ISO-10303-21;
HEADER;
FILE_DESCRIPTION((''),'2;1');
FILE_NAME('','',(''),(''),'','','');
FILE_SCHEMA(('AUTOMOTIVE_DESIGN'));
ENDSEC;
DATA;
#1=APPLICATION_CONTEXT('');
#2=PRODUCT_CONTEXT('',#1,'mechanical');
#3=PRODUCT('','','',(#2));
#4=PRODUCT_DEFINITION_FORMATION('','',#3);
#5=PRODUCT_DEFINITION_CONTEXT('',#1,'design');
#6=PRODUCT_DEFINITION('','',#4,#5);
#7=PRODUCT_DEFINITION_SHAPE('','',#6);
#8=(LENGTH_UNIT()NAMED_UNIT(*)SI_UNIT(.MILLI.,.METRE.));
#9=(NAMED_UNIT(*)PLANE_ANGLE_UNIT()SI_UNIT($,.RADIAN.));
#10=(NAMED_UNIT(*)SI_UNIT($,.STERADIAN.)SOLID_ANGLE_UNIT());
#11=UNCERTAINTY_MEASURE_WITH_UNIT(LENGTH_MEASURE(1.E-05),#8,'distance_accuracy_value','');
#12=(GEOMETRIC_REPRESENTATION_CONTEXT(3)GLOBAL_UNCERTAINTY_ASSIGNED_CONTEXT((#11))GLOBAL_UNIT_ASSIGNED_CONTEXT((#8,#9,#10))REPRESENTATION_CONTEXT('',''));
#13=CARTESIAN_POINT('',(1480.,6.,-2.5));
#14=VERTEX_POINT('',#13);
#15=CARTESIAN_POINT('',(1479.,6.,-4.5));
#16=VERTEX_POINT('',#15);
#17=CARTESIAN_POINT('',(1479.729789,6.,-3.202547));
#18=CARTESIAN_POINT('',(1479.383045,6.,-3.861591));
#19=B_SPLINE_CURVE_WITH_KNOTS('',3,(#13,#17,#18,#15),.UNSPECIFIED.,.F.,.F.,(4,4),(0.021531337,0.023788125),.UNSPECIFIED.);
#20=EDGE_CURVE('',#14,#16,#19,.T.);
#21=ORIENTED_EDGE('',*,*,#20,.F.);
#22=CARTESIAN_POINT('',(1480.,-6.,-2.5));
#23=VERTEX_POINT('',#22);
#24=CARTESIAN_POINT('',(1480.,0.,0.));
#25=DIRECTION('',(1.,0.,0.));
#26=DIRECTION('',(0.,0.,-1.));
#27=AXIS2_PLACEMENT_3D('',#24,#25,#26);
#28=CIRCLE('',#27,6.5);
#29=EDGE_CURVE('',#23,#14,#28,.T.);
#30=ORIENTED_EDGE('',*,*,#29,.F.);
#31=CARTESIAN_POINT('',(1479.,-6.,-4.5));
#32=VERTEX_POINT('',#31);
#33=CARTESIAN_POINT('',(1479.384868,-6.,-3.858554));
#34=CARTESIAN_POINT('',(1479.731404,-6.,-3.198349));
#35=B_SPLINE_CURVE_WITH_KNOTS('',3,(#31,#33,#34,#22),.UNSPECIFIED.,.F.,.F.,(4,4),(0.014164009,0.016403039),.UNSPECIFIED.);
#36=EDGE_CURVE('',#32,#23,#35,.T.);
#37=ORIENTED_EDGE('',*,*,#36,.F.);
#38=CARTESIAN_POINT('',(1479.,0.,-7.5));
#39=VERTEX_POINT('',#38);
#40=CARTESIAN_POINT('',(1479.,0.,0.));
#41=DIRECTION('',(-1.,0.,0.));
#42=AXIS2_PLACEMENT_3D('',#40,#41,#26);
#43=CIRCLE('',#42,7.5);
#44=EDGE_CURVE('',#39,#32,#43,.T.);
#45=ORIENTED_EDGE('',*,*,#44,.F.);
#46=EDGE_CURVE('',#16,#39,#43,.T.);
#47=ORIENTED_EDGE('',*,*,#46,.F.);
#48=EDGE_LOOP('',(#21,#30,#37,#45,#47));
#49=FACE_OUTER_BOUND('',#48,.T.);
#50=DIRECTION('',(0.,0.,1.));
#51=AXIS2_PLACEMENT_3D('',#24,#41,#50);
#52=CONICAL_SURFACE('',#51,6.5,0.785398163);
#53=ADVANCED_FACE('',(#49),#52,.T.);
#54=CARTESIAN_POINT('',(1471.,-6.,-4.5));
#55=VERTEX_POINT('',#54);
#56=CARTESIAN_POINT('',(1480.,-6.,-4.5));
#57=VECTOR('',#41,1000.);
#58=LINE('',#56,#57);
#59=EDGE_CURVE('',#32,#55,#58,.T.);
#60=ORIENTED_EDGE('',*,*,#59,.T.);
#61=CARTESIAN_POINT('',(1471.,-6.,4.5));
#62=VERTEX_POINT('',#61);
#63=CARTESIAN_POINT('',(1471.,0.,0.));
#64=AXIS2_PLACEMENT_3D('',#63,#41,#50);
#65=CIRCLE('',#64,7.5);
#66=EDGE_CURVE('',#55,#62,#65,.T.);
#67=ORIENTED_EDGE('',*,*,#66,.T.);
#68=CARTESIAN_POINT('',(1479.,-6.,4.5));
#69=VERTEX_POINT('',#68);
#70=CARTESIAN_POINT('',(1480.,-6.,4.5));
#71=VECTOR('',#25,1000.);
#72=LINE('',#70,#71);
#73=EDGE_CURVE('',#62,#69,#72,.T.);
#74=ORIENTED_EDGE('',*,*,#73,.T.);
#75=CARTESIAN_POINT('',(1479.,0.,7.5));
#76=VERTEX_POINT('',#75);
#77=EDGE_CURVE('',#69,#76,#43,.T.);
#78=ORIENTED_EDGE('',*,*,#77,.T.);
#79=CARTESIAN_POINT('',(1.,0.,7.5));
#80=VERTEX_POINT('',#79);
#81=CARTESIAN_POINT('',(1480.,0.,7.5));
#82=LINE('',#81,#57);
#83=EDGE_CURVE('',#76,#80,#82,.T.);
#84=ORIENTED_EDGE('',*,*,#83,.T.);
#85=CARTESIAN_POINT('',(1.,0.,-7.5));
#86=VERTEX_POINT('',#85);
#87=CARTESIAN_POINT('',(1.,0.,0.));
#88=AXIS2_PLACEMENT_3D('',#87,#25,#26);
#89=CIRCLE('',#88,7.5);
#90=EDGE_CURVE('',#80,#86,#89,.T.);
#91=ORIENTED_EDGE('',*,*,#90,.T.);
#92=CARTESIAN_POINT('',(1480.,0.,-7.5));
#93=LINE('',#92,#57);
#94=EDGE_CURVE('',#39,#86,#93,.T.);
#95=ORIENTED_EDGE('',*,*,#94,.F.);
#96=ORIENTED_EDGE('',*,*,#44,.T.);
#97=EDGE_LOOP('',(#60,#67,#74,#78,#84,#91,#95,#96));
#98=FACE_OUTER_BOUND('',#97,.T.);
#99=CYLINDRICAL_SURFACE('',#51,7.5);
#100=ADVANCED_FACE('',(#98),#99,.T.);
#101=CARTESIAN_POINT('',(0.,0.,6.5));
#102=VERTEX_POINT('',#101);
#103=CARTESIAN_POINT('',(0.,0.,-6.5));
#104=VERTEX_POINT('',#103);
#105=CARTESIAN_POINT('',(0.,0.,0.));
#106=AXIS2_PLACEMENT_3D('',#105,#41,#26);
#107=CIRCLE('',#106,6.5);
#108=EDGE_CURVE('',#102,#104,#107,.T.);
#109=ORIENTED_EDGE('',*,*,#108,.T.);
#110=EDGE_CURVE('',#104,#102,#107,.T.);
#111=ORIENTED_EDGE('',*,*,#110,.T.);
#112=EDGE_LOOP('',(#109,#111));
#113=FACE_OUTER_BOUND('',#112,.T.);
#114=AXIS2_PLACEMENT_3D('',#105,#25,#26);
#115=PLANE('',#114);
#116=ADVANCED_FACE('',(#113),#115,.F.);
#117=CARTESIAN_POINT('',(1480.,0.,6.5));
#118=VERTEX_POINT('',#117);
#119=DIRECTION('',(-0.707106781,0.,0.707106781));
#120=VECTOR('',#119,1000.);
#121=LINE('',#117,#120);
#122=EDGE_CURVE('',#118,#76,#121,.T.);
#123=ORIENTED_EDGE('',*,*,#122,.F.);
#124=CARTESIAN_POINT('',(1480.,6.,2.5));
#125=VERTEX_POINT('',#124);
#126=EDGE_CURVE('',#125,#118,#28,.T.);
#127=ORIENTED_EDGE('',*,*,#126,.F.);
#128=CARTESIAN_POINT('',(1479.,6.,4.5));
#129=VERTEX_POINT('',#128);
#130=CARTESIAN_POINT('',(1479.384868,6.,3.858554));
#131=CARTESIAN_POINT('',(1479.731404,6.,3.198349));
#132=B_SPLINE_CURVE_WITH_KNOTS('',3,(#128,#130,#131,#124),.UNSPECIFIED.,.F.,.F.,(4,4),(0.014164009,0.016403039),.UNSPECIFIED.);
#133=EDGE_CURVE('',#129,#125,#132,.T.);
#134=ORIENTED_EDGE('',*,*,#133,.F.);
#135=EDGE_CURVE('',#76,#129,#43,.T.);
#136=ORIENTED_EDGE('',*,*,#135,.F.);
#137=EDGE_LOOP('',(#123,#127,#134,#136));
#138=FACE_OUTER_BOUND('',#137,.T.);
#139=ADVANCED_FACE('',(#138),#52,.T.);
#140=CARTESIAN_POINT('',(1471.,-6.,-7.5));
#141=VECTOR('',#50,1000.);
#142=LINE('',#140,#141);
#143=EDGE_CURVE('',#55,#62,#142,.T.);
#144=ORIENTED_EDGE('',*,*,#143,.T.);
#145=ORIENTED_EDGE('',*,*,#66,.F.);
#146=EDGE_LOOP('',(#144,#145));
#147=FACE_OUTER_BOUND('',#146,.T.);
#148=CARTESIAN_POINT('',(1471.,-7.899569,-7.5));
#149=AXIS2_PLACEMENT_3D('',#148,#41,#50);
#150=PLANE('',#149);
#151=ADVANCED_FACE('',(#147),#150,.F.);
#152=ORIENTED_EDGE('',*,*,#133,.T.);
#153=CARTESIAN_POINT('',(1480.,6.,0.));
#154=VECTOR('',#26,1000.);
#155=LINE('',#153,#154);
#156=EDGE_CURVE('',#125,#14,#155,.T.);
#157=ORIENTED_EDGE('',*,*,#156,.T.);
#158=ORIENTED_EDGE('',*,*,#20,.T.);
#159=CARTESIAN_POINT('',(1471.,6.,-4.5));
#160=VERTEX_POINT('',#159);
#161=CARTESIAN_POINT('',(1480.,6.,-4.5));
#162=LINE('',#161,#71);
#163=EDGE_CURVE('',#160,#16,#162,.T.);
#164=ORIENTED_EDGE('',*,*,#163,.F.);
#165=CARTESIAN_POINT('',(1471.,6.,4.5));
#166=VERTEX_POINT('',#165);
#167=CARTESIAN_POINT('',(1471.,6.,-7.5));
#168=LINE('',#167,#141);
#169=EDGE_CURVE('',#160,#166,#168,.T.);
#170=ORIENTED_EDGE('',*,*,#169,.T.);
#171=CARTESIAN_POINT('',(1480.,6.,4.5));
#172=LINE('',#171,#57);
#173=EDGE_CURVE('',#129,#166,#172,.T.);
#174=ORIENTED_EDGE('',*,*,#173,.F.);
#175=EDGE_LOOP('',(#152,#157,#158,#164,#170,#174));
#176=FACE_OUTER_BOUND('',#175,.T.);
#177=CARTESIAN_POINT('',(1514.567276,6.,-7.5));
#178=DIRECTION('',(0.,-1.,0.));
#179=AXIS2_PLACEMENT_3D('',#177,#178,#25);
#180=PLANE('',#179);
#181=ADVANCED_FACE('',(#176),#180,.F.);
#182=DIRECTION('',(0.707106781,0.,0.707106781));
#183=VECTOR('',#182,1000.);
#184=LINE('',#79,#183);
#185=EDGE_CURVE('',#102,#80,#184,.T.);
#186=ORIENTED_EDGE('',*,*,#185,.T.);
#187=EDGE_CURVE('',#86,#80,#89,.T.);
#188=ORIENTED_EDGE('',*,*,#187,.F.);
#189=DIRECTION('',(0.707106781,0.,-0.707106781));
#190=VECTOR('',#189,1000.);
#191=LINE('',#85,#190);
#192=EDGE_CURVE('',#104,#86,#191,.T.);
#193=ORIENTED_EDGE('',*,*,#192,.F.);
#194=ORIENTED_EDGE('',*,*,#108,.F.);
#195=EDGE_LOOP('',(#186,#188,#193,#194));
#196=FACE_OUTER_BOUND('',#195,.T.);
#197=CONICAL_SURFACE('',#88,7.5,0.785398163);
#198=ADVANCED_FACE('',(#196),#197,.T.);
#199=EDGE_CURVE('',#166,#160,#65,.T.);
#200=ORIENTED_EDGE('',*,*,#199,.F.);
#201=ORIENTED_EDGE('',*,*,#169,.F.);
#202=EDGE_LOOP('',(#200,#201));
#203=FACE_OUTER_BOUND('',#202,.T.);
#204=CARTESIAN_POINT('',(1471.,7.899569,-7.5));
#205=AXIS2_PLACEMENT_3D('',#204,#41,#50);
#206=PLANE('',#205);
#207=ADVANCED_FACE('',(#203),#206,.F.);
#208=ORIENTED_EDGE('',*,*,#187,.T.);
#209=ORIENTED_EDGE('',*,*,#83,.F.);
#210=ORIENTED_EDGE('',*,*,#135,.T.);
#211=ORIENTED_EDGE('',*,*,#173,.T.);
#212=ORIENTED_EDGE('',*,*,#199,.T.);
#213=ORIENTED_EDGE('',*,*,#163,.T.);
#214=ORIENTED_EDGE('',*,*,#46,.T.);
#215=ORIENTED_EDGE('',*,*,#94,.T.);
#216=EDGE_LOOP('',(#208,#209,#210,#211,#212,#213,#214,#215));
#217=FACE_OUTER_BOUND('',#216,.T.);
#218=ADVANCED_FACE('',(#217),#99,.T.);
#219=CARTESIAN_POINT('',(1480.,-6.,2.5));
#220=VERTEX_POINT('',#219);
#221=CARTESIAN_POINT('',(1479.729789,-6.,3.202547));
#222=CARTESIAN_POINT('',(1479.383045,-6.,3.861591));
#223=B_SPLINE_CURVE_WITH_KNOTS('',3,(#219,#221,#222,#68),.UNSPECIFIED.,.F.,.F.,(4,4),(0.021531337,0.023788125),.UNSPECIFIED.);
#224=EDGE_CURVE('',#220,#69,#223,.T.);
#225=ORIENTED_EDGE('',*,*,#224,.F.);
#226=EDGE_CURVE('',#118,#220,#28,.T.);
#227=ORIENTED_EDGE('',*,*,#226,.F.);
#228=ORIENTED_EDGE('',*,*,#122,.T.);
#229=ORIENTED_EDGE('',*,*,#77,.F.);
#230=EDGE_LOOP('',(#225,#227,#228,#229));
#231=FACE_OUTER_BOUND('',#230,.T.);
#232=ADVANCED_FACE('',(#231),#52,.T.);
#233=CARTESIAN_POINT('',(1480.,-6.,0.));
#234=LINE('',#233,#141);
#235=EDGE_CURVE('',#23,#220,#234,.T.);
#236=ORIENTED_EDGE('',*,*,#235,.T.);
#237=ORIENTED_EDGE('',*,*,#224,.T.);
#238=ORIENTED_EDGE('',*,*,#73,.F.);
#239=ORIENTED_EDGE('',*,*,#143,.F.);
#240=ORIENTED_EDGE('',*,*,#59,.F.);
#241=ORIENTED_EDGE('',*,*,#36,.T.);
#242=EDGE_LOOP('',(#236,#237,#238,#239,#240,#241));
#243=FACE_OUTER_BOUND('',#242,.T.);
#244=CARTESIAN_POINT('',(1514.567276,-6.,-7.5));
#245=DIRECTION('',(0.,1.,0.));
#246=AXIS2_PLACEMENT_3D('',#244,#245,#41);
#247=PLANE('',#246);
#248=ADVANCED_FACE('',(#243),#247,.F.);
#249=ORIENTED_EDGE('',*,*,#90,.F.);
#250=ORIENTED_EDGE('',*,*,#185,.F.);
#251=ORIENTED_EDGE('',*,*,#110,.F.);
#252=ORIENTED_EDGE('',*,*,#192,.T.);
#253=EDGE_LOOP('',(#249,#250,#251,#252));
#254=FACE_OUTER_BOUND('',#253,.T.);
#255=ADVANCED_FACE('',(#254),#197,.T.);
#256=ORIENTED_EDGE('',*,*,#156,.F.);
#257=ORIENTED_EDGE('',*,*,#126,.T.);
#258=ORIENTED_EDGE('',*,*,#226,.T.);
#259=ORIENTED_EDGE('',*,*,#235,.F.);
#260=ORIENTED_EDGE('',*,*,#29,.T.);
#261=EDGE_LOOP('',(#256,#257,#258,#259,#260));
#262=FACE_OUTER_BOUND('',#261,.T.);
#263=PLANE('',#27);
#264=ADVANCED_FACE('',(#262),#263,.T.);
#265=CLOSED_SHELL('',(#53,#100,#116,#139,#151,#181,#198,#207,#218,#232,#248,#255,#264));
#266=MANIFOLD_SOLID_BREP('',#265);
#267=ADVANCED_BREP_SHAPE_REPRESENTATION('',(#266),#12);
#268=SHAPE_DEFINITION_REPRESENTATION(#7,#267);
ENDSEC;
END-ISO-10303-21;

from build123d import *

# Parameters (mm, degrees)
SKETCH1_R               = 7.5
BOSS_EXTRUDE1_DEPTH     = 1480
CHAMFER1_SIZE           = 1
CUT_EXTRUDE1_DEPTH      = 1481.038006269
CUT_EXTRUDE1_DEPTH_BACK = 1481.038006269
SKETCH8_W               = 43.567276196
SKETCH8_H               = 1.89956865


with BuildPart() as part:
    # Sketch1 → Boss-Extrude1 (new body)
    with BuildSketch(Plane(origin=(0, 0, 0), x_dir=(0, 0, -1), z_dir=(1, 0, 0))):
        Circle(SKETCH1_R)
    extrude(amount=BOSS_EXTRUDE1_DEPTH)

    # Chamfer1
    chamfer1_edges = [part.edges().sort_by_distance(p)[0] for p in [
        (0, 0, 7.5),
        (1480, 0, 7.5),
    ]]
    chamfer(chamfer1_edges, length=CHAMFER1_SIZE)

    # Sketch8 → Cut-Extrude1 (cut, two sides: drawn at the far end of the back side and taken through both)
    with BuildSketch(Plane.XY.offset(-CUT_EXTRUDE1_DEPTH_BACK)):
        with Locations((1492.783638098, 6.949784325)):
            Rectangle(SKETCH8_W, SKETCH8_H)
        with Locations((1492.783638098, -6.949784325)):
            Rectangle(SKETCH8_W, SKETCH8_H)
    extrude(amount=CUT_EXTRUDE1_DEPTH + CUT_EXTRUDE1_DEPTH_BACK, mode=Mode.SUBTRACT)


solid = part.part
